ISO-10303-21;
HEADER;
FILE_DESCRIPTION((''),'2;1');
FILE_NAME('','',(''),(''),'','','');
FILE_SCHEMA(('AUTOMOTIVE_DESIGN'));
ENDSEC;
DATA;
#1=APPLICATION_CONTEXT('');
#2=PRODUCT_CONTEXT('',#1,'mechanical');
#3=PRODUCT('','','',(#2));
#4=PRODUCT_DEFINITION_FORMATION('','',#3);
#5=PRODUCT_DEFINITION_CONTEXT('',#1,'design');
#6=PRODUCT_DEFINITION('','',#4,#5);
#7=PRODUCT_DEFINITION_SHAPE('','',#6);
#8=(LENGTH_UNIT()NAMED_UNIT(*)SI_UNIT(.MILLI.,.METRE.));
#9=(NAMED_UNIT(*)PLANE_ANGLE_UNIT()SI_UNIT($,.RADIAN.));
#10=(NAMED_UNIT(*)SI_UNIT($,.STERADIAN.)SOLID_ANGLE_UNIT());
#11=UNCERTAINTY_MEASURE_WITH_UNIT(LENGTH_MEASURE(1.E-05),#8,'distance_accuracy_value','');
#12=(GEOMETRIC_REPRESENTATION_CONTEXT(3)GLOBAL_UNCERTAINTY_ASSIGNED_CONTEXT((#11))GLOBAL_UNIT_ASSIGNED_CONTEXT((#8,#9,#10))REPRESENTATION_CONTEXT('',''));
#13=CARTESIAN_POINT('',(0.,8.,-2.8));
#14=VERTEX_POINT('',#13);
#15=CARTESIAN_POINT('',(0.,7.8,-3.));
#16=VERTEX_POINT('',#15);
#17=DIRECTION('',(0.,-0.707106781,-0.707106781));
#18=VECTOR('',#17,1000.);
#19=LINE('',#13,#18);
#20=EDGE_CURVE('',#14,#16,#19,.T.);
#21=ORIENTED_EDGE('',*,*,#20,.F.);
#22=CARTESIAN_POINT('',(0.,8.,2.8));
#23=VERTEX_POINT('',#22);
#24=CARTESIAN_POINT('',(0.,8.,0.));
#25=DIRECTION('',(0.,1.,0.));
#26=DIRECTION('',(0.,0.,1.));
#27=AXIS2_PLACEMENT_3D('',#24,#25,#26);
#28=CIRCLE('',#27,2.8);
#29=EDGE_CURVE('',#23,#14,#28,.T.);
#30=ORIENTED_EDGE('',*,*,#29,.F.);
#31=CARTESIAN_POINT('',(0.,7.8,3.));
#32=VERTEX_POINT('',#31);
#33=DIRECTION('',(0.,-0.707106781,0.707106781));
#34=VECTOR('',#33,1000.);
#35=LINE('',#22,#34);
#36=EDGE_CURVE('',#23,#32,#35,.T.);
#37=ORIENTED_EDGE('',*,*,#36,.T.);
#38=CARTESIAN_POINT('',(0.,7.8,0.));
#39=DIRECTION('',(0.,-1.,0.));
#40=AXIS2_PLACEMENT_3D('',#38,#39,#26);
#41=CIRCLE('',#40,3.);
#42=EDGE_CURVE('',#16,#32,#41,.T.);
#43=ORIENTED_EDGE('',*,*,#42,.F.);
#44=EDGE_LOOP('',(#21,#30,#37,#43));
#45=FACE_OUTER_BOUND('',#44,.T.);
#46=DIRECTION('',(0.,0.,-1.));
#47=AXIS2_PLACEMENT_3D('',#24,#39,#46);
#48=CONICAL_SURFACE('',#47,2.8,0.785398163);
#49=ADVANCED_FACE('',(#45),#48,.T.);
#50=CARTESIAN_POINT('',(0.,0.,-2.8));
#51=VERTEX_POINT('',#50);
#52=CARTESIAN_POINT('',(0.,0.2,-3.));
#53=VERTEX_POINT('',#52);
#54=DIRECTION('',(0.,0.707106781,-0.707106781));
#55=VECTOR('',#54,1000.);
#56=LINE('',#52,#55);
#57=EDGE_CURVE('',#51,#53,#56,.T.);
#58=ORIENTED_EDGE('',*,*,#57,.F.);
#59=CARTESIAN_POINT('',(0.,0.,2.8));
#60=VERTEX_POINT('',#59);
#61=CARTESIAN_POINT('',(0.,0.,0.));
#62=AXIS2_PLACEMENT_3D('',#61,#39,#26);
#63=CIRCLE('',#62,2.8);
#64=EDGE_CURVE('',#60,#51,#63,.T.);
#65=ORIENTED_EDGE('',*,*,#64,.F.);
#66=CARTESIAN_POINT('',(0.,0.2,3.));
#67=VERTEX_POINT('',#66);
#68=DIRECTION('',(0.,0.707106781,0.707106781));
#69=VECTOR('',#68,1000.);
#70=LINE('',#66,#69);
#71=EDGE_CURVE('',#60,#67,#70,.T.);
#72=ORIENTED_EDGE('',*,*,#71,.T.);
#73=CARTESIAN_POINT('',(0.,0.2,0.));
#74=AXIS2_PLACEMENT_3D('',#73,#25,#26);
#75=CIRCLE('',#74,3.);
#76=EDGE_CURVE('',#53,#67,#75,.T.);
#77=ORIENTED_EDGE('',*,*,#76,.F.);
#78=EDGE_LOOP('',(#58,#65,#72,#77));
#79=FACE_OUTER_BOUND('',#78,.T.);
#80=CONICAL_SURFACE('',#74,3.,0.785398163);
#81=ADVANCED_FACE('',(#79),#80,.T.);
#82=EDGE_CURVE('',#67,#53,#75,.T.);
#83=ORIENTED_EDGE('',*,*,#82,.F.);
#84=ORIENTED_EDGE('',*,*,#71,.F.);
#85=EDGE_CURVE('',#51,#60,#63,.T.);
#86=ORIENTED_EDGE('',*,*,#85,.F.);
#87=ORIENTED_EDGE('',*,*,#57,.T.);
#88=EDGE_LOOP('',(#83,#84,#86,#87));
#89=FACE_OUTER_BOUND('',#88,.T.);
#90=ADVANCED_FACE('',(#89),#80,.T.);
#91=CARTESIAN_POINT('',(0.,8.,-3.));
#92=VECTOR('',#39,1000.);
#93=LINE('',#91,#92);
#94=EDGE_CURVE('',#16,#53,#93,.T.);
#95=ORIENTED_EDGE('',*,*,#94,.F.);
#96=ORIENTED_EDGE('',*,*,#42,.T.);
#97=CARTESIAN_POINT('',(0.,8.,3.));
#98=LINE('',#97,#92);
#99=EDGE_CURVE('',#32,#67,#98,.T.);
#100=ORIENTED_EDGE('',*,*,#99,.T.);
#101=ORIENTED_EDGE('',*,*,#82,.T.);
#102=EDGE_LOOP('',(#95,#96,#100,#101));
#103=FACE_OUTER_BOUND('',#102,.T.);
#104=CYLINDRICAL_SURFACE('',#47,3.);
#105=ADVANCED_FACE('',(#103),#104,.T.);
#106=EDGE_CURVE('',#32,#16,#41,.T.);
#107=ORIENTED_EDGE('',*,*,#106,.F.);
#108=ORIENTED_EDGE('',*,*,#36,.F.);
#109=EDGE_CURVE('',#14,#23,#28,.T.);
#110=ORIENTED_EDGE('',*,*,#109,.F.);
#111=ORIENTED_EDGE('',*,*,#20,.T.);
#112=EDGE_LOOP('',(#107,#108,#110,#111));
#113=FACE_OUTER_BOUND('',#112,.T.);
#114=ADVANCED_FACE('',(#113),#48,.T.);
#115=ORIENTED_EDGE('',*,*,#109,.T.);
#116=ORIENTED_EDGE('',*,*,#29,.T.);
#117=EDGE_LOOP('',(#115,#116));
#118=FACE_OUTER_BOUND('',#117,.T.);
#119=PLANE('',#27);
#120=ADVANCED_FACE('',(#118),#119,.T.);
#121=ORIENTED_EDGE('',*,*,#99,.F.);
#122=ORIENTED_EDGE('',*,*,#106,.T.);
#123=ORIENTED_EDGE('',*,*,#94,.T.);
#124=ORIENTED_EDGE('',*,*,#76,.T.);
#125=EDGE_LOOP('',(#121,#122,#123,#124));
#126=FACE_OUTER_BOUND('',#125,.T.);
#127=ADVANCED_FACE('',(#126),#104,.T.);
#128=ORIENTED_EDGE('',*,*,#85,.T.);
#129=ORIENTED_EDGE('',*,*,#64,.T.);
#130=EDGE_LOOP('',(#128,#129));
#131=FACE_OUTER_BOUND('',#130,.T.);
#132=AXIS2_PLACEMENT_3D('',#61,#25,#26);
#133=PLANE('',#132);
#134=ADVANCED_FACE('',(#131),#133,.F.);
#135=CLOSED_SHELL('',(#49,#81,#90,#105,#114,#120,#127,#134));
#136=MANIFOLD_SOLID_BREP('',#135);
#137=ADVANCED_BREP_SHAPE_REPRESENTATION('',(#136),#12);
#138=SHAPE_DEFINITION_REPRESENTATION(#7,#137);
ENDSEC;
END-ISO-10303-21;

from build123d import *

# Parameters (mm, degrees)
SKETCH1_R           = 3
BOSS_EXTRUDE1_DEPTH = 8
CHAMFER1_SIZE       = 0.2


with BuildPart() as part:
    # Sketch1 → Boss-Extrude1 (new body)
    with BuildSketch(Plane(origin=(0, 0, 0), x_dir=(1, 0, 0), z_dir=(0, 1, 0))):
        with Locations(Location((0, 0, 0), (0, 0, 270))):
            Circle(SKETCH1_R)
    extrude(amount=BOSS_EXTRUDE1_DEPTH)

    # Chamfer1
    chamfer1_edges = [part.edges().sort_by_distance(p)[0] for p in [
        (0, 0, -3),
        (0, 8, -3),
    ]]
    chamfer(chamfer1_edges, length=CHAMFER1_SIZE)


solid = part.part
